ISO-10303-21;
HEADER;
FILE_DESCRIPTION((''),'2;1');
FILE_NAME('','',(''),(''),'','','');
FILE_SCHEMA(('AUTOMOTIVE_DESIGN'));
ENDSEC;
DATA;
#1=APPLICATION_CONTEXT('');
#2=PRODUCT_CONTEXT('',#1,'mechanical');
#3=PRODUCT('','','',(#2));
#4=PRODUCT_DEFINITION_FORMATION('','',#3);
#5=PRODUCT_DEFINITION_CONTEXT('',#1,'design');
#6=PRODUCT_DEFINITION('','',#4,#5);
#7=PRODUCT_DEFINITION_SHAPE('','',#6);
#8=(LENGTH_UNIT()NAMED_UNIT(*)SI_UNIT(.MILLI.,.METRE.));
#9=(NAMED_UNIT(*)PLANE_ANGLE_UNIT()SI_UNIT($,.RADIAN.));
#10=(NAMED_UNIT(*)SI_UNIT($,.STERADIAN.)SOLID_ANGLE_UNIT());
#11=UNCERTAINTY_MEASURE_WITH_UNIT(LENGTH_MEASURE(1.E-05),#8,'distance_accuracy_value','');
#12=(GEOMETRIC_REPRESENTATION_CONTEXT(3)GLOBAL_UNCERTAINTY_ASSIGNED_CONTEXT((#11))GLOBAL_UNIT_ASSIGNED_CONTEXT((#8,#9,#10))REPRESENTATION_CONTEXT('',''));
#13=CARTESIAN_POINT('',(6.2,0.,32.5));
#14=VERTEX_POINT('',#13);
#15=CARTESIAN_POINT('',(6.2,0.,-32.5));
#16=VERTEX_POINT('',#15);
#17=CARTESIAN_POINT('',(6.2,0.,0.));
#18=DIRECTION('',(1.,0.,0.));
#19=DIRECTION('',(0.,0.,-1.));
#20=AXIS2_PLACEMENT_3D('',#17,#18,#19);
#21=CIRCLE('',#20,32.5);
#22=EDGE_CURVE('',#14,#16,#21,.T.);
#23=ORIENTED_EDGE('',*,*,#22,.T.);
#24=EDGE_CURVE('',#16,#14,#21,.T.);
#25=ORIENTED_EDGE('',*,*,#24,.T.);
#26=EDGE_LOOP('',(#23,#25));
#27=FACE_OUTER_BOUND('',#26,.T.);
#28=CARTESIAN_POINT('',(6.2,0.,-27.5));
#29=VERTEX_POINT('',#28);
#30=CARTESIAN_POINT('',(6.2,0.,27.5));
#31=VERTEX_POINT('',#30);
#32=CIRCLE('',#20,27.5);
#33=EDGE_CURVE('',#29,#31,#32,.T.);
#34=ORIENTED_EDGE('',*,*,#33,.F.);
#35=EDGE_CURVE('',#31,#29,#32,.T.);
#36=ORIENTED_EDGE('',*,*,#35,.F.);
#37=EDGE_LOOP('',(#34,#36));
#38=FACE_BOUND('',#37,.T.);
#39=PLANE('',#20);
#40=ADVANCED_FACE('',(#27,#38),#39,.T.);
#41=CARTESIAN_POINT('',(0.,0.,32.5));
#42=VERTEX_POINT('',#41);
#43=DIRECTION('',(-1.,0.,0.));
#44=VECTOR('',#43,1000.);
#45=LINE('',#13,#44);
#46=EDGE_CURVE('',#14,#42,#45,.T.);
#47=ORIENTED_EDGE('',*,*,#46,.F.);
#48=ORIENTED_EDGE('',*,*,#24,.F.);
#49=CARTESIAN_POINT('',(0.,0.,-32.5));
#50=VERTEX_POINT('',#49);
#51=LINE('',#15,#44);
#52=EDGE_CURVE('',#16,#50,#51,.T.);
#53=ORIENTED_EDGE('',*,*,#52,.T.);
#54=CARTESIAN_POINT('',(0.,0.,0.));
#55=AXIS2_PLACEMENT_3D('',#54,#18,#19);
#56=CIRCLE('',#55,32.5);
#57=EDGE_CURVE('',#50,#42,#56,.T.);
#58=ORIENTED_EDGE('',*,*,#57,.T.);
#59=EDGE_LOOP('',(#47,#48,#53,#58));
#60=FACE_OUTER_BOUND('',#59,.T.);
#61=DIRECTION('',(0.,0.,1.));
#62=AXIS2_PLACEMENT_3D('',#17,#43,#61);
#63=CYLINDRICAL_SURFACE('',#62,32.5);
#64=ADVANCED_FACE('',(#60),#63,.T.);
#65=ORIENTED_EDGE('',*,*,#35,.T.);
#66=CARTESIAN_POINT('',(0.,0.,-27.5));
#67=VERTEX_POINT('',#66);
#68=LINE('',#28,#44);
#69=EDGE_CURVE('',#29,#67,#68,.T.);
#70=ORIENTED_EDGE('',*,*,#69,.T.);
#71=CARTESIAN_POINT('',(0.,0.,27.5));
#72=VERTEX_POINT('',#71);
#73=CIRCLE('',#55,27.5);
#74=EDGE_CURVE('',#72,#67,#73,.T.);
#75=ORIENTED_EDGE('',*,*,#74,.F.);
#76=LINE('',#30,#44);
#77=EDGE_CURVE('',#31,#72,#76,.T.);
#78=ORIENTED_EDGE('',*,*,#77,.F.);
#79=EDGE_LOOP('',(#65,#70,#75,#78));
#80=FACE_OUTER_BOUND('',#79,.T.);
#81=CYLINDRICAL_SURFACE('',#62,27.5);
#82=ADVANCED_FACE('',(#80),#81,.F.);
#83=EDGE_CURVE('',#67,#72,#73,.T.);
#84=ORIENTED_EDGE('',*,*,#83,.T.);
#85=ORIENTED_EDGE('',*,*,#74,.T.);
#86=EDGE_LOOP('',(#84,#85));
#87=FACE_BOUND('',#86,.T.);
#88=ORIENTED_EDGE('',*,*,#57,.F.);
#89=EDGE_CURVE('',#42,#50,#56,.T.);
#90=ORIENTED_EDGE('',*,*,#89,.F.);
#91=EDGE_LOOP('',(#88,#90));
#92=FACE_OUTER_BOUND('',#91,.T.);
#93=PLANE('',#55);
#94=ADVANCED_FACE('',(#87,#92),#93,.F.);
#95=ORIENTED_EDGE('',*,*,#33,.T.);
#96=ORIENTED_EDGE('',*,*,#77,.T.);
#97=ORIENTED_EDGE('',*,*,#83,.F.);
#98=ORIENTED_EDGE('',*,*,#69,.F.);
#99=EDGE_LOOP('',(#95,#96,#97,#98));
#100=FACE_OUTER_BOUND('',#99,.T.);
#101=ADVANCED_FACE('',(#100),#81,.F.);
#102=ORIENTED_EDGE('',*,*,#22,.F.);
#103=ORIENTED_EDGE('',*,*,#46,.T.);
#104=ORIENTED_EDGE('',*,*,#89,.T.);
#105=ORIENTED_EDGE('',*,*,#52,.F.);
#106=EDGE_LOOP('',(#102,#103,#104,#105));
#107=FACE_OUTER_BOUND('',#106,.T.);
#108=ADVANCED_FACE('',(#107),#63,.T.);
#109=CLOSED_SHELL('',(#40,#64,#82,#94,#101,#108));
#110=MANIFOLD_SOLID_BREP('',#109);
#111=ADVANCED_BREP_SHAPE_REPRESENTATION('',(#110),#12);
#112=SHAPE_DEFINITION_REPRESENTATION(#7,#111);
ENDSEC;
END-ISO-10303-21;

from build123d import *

# Parameters (mm, degrees)
SKETCH2_R           = 32.5
SKETCH2_R_2         = 27.5
BOSS_EXTRUDE1_DEPTH = 6.2


with BuildPart() as part:
    # Sketch2 → Boss-Extrude1 (new body)
    with BuildSketch(Plane(origin=(0, 0, 0), x_dir=(0, 0, -1), z_dir=(1, 0, 0))):
        with Locations(Location((0, 0, 0), (0, 0, 180))):
            Circle(SKETCH2_R)
        with Locations(Location((0, 0, 0), (0, 0, 180))):
            Circle(SKETCH2_R_2, mode=Mode.SUBTRACT)
    extrude(amount=BOSS_EXTRUDE1_DEPTH)


solid = part.part
